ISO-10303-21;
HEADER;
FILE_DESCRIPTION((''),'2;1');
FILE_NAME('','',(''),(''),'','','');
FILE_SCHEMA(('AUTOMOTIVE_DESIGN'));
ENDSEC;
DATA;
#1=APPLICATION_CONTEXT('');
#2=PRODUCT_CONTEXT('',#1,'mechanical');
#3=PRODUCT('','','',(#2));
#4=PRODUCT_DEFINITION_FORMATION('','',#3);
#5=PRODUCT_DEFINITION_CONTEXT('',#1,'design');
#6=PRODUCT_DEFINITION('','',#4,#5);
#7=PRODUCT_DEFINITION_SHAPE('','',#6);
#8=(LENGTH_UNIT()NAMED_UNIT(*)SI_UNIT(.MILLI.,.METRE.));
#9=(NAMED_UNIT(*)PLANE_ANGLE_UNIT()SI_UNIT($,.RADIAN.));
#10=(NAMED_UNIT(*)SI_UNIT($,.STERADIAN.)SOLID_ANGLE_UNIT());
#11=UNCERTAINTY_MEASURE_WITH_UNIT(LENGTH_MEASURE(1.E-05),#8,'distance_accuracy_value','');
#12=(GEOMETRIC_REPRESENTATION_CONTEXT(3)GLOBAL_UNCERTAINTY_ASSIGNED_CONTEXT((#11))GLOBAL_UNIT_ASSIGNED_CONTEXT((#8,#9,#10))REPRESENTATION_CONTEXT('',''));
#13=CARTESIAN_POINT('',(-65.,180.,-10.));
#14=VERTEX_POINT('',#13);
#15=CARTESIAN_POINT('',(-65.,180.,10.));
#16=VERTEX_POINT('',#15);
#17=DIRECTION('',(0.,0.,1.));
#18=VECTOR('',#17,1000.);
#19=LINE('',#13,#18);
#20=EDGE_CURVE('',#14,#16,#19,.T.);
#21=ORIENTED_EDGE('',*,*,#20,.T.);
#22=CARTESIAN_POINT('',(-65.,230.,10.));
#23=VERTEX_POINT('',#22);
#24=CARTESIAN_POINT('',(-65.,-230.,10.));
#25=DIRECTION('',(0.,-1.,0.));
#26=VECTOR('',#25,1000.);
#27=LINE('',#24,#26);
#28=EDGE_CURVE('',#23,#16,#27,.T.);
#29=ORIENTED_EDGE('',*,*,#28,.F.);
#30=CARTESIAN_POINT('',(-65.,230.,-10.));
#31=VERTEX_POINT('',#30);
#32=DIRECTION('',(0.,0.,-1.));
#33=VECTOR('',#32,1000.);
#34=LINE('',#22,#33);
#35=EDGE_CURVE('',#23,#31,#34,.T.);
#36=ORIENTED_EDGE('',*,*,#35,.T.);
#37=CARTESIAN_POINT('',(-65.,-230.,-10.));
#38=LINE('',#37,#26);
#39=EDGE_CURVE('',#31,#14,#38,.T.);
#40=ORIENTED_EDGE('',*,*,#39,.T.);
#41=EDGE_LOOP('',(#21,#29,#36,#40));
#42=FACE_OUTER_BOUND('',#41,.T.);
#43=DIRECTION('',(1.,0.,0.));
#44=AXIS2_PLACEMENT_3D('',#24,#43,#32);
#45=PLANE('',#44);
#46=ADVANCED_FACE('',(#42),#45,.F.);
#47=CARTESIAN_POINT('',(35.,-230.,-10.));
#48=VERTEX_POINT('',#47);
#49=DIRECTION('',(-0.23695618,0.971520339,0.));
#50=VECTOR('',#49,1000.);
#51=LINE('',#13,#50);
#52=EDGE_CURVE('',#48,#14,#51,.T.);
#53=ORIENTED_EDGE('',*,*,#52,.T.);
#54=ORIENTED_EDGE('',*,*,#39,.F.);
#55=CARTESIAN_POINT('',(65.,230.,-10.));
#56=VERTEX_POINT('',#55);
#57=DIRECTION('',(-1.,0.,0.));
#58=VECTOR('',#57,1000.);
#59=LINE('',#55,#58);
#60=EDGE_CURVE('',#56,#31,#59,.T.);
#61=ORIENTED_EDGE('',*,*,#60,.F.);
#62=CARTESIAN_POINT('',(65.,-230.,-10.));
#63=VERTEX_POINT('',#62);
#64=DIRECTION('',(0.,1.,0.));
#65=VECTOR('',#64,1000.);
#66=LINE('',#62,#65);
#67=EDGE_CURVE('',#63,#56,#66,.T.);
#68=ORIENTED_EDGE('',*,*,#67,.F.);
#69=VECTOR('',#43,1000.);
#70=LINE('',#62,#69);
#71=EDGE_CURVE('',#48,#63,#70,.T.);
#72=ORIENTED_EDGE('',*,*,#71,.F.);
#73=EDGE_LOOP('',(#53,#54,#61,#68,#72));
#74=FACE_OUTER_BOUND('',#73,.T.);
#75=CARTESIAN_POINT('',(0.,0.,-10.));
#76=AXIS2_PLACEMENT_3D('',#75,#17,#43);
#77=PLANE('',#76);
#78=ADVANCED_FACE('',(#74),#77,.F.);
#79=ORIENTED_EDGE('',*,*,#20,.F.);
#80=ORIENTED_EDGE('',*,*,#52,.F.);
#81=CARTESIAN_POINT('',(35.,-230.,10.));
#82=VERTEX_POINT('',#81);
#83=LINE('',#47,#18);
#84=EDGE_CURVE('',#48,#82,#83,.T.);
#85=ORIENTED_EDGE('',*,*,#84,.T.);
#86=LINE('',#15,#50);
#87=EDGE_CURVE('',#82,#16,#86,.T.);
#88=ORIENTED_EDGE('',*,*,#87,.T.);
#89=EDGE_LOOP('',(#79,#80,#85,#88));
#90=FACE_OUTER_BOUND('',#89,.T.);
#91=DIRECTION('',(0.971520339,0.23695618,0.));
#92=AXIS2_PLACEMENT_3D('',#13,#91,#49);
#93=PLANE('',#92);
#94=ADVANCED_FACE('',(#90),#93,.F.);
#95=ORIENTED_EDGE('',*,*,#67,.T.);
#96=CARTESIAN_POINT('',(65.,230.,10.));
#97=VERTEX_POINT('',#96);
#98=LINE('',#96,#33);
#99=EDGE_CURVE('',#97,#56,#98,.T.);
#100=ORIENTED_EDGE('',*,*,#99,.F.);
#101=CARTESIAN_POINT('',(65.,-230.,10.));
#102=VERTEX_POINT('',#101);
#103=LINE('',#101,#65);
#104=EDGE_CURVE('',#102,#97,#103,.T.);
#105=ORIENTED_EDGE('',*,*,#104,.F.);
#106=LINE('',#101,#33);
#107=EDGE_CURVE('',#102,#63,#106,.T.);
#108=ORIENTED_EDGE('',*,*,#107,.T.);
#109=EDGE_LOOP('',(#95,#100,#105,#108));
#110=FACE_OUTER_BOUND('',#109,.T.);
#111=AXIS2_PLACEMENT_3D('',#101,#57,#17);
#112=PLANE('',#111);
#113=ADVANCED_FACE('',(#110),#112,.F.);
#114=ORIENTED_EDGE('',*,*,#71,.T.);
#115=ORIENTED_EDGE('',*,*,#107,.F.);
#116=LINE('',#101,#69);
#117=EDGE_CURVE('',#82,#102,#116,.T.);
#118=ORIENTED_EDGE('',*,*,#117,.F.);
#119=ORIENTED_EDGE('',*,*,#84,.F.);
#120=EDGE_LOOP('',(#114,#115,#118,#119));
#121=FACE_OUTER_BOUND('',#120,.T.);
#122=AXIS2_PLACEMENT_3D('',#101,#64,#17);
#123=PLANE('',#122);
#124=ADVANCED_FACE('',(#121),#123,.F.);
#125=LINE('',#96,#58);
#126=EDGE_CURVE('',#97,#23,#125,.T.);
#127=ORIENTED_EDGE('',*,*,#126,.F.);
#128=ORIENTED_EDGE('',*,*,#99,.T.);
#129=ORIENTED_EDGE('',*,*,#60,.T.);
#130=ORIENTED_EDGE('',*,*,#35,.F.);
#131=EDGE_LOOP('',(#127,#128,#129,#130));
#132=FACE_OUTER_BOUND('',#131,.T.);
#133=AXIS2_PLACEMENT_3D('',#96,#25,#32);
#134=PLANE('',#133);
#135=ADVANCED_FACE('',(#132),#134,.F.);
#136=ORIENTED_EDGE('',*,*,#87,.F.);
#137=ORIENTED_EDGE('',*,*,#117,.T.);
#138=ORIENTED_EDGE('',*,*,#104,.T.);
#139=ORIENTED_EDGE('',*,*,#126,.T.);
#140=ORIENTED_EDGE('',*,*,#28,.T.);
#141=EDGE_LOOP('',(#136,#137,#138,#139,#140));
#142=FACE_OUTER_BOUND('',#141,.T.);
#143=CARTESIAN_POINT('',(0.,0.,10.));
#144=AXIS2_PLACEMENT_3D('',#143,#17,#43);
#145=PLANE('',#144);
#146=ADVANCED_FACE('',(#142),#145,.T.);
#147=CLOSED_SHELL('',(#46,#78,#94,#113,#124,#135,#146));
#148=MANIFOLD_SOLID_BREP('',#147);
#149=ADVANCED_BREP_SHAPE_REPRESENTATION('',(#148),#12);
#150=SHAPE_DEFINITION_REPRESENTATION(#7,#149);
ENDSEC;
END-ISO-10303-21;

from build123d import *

# Parameters (mm, degrees)
SKETCH1_W           = 130
SKETCH1_H           = 460
BOSS_EXTRUDE1_DEPTH = 10
CUT_EXTRUDE1_DEPTH  = 240.843699104


with BuildPart() as part:
    # Sketch1 → Boss-Extrude1 (new, symmetric)
    with BuildSketch(Plane.XY):
        Rectangle(SKETCH1_W, SKETCH1_H)
    extrude(amount=BOSS_EXTRUDE1_DEPTH, both=True)

    # Sketch2 → Cut-Extrude1 (cut, through all)
    with BuildSketch(Plane.XY.offset(10)):
        Polygon((-65, 180), (35, -230), (-65, -230), align=None)
    extrude(amount=-CUT_EXTRUDE1_DEPTH, mode=Mode.SUBTRACT)


solid = part.part
